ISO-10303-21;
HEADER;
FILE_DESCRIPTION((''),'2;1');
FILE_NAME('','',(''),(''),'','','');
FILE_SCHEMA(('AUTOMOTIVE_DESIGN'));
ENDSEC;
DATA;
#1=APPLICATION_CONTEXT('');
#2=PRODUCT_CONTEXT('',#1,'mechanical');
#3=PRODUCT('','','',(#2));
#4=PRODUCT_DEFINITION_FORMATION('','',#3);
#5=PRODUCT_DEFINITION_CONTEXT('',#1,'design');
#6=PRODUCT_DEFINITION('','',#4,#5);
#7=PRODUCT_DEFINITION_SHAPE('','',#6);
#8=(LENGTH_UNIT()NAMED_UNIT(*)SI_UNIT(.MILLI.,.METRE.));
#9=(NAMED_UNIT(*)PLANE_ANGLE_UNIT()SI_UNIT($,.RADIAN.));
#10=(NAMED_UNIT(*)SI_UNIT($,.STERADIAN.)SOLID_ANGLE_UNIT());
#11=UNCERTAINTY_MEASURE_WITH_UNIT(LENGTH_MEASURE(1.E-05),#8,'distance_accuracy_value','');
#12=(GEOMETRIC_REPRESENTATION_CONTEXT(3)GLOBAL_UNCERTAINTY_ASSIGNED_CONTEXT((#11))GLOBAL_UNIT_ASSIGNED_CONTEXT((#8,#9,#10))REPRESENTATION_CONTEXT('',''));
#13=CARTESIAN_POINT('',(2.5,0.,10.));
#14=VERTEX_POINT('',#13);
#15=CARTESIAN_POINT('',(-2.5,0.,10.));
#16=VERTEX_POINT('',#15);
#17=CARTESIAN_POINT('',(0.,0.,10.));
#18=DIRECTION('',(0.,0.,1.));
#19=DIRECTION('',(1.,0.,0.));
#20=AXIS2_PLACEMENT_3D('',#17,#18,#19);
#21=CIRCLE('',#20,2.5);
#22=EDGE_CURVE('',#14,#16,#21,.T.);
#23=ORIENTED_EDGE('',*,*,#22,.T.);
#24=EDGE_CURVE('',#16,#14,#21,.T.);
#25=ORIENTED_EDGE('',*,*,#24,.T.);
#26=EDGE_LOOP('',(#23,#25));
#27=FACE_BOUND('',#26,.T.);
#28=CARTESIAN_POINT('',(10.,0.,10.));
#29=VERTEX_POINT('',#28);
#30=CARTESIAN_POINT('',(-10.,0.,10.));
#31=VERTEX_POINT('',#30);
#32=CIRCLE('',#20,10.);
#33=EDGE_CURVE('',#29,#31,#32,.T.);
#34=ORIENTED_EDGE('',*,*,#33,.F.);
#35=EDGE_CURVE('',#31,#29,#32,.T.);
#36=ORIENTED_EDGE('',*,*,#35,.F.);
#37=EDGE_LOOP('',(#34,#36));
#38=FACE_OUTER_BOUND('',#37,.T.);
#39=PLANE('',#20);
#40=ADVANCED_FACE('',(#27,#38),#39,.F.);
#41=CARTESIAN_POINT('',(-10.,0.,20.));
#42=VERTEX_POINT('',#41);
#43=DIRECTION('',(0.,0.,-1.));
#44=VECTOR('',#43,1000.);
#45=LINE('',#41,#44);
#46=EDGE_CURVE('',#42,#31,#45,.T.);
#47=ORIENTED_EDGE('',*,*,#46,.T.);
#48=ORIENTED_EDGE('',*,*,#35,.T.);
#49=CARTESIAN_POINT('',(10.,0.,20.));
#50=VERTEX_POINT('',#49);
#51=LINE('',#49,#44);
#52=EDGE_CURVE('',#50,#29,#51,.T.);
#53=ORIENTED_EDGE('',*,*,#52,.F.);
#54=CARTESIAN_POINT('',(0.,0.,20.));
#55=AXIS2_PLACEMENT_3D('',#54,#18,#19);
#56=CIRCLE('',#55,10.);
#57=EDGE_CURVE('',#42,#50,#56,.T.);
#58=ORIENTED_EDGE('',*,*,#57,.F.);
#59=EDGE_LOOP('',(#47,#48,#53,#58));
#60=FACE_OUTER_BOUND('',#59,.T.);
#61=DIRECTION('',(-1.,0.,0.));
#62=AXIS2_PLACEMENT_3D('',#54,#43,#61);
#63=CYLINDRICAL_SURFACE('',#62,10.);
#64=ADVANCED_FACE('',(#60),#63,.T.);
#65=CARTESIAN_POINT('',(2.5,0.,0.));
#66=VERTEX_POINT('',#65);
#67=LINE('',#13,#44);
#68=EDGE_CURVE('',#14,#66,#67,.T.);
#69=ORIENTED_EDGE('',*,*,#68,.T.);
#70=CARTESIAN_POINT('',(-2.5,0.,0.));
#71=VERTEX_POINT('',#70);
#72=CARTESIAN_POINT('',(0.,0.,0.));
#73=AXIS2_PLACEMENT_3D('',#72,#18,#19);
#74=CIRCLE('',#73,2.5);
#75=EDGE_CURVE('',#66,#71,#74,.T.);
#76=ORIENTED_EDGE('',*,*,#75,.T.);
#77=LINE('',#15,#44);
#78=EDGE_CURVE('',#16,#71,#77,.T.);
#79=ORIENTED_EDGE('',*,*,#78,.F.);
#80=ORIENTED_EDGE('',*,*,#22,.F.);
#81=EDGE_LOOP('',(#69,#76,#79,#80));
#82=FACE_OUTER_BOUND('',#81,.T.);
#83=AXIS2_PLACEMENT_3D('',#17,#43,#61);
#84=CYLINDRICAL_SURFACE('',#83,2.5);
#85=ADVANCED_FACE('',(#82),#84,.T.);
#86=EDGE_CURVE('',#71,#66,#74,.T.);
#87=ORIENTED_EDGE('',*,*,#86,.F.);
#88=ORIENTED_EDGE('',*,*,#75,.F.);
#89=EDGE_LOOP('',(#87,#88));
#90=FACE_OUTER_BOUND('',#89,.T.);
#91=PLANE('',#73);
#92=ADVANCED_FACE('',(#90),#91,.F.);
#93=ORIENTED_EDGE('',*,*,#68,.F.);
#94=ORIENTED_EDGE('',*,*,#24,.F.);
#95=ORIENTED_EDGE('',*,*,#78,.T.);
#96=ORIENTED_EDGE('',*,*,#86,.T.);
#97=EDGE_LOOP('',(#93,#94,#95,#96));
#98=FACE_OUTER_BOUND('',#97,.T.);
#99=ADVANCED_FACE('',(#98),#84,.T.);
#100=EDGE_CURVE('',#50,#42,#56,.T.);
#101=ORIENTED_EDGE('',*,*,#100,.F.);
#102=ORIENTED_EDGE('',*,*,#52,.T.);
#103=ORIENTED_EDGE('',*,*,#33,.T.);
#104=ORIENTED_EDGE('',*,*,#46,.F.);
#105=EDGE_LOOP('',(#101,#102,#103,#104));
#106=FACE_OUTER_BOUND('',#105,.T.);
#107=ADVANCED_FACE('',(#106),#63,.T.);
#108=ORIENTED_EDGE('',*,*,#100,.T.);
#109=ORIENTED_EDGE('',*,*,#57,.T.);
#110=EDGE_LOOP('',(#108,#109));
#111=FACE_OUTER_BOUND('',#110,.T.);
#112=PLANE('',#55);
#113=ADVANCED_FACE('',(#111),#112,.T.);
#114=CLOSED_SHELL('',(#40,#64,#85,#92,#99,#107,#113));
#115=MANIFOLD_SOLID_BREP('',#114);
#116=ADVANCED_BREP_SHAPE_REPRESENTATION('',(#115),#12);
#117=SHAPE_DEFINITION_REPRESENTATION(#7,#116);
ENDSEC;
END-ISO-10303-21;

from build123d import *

# Parameters (mm, degrees)
SKETCH1_R           = 2.5
BOSS_EXTRUDE1_DEPTH = 10
SKETCH2_R           = 10
BOSS_EXTRUDE2_DEPTH = 10


with BuildPart() as part:
    # Sketch1 → Boss-Extrude1 (new body)
    with BuildSketch(Plane.XY):
        Circle(SKETCH1_R)
    extrude(amount=BOSS_EXTRUDE1_DEPTH)

    # Sketch2 → Boss-Extrude2 (add)
    with BuildSketch(Plane.XY.offset(10)):
        Circle(SKETCH2_R)
    extrude(amount=BOSS_EXTRUDE2_DEPTH)


solid = part.part
